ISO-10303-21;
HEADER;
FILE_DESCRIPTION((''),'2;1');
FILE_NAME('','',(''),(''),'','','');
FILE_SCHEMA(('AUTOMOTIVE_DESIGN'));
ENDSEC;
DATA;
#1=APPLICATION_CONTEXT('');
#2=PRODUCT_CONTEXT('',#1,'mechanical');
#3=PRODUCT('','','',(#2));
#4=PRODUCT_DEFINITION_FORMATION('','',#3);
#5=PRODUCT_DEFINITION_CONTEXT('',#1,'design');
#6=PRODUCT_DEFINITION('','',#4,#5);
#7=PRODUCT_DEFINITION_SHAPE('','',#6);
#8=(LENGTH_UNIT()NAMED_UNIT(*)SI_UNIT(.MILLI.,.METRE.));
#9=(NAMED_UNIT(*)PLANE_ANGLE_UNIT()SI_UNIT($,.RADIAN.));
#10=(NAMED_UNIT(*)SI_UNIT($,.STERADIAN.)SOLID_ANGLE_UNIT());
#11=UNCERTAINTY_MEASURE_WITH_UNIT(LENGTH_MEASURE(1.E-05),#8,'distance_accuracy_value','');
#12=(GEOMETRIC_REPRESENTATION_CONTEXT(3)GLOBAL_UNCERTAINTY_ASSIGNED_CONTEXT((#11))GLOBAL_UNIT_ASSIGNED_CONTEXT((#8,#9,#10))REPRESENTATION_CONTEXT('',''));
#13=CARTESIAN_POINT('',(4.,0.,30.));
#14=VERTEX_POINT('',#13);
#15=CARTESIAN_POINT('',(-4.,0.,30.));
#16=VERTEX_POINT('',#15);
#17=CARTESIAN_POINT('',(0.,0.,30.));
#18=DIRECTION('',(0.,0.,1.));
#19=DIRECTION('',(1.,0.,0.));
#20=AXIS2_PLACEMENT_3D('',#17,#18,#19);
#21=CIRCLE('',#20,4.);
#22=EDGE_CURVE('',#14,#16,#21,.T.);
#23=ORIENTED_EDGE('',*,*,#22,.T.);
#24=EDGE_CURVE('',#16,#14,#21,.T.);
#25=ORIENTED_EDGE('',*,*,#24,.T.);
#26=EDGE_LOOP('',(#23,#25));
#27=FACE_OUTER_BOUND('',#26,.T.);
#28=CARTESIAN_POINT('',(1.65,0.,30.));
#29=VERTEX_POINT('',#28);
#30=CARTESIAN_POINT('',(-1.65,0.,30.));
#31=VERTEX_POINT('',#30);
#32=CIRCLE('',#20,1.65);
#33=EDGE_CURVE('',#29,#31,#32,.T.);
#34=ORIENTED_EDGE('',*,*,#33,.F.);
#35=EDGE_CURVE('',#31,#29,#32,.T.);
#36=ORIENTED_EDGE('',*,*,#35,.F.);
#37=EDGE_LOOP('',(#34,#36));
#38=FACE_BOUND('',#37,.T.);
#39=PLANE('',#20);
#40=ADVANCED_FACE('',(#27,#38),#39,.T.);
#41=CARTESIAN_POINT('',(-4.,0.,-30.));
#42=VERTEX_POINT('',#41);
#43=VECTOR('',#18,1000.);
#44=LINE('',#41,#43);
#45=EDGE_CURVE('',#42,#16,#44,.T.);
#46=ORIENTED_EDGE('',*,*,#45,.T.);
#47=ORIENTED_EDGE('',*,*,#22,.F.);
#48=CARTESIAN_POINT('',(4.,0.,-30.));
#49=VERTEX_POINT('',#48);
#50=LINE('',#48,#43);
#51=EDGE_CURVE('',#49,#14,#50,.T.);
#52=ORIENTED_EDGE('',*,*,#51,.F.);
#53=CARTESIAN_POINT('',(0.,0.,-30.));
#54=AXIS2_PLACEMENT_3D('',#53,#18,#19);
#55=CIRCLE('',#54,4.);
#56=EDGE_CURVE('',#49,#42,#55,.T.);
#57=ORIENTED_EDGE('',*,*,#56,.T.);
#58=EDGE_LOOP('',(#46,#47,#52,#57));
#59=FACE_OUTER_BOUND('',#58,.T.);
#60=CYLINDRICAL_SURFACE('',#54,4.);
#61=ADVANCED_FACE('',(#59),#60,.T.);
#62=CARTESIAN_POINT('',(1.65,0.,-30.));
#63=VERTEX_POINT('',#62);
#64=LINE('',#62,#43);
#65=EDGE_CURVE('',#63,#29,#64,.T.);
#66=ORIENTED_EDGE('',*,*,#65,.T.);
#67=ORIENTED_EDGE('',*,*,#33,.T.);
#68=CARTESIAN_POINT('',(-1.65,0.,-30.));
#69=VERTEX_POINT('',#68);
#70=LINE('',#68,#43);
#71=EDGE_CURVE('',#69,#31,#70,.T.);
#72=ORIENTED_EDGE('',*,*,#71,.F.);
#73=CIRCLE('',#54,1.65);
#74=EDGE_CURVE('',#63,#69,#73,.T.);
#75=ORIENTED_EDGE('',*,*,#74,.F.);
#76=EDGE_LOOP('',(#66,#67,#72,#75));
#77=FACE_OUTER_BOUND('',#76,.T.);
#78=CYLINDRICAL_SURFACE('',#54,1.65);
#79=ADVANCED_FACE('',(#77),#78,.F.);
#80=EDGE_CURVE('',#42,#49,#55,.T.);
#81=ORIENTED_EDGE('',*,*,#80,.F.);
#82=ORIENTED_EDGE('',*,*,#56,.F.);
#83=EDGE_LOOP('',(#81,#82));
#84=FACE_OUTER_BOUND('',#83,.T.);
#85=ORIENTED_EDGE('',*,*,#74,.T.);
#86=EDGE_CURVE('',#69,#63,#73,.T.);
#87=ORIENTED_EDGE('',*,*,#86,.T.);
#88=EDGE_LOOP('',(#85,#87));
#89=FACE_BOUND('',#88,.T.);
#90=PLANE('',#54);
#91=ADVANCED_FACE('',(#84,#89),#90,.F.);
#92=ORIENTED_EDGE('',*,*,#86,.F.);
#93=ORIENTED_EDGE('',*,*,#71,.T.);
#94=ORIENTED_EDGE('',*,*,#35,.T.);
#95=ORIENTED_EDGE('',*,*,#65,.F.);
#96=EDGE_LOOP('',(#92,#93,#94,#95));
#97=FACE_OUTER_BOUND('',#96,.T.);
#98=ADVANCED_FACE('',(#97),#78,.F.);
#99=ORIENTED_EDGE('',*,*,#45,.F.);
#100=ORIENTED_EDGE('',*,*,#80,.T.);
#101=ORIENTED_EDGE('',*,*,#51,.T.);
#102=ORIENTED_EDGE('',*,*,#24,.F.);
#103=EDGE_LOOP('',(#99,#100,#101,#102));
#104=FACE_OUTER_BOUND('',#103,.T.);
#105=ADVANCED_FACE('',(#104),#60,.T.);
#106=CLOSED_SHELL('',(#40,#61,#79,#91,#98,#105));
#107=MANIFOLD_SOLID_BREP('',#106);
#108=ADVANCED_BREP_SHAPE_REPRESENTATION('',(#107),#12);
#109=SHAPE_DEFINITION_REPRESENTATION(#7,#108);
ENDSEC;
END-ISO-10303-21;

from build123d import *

# Parameters (mm, degrees)
SKETCH_1_R      = 4
SKETCH_1_R_2    = 1.65
EXTRUDE_1_DEPTH = 30


with BuildPart() as part:
    # 草图1 → 凸台-拉伸1 (new, symmetric)
    with BuildSketch(Plane.XY):
        Circle(SKETCH_1_R)
        Circle(SKETCH_1_R_2, mode=Mode.SUBTRACT)
    extrude(amount=EXTRUDE_1_DEPTH, both=True)


solid = part.part
